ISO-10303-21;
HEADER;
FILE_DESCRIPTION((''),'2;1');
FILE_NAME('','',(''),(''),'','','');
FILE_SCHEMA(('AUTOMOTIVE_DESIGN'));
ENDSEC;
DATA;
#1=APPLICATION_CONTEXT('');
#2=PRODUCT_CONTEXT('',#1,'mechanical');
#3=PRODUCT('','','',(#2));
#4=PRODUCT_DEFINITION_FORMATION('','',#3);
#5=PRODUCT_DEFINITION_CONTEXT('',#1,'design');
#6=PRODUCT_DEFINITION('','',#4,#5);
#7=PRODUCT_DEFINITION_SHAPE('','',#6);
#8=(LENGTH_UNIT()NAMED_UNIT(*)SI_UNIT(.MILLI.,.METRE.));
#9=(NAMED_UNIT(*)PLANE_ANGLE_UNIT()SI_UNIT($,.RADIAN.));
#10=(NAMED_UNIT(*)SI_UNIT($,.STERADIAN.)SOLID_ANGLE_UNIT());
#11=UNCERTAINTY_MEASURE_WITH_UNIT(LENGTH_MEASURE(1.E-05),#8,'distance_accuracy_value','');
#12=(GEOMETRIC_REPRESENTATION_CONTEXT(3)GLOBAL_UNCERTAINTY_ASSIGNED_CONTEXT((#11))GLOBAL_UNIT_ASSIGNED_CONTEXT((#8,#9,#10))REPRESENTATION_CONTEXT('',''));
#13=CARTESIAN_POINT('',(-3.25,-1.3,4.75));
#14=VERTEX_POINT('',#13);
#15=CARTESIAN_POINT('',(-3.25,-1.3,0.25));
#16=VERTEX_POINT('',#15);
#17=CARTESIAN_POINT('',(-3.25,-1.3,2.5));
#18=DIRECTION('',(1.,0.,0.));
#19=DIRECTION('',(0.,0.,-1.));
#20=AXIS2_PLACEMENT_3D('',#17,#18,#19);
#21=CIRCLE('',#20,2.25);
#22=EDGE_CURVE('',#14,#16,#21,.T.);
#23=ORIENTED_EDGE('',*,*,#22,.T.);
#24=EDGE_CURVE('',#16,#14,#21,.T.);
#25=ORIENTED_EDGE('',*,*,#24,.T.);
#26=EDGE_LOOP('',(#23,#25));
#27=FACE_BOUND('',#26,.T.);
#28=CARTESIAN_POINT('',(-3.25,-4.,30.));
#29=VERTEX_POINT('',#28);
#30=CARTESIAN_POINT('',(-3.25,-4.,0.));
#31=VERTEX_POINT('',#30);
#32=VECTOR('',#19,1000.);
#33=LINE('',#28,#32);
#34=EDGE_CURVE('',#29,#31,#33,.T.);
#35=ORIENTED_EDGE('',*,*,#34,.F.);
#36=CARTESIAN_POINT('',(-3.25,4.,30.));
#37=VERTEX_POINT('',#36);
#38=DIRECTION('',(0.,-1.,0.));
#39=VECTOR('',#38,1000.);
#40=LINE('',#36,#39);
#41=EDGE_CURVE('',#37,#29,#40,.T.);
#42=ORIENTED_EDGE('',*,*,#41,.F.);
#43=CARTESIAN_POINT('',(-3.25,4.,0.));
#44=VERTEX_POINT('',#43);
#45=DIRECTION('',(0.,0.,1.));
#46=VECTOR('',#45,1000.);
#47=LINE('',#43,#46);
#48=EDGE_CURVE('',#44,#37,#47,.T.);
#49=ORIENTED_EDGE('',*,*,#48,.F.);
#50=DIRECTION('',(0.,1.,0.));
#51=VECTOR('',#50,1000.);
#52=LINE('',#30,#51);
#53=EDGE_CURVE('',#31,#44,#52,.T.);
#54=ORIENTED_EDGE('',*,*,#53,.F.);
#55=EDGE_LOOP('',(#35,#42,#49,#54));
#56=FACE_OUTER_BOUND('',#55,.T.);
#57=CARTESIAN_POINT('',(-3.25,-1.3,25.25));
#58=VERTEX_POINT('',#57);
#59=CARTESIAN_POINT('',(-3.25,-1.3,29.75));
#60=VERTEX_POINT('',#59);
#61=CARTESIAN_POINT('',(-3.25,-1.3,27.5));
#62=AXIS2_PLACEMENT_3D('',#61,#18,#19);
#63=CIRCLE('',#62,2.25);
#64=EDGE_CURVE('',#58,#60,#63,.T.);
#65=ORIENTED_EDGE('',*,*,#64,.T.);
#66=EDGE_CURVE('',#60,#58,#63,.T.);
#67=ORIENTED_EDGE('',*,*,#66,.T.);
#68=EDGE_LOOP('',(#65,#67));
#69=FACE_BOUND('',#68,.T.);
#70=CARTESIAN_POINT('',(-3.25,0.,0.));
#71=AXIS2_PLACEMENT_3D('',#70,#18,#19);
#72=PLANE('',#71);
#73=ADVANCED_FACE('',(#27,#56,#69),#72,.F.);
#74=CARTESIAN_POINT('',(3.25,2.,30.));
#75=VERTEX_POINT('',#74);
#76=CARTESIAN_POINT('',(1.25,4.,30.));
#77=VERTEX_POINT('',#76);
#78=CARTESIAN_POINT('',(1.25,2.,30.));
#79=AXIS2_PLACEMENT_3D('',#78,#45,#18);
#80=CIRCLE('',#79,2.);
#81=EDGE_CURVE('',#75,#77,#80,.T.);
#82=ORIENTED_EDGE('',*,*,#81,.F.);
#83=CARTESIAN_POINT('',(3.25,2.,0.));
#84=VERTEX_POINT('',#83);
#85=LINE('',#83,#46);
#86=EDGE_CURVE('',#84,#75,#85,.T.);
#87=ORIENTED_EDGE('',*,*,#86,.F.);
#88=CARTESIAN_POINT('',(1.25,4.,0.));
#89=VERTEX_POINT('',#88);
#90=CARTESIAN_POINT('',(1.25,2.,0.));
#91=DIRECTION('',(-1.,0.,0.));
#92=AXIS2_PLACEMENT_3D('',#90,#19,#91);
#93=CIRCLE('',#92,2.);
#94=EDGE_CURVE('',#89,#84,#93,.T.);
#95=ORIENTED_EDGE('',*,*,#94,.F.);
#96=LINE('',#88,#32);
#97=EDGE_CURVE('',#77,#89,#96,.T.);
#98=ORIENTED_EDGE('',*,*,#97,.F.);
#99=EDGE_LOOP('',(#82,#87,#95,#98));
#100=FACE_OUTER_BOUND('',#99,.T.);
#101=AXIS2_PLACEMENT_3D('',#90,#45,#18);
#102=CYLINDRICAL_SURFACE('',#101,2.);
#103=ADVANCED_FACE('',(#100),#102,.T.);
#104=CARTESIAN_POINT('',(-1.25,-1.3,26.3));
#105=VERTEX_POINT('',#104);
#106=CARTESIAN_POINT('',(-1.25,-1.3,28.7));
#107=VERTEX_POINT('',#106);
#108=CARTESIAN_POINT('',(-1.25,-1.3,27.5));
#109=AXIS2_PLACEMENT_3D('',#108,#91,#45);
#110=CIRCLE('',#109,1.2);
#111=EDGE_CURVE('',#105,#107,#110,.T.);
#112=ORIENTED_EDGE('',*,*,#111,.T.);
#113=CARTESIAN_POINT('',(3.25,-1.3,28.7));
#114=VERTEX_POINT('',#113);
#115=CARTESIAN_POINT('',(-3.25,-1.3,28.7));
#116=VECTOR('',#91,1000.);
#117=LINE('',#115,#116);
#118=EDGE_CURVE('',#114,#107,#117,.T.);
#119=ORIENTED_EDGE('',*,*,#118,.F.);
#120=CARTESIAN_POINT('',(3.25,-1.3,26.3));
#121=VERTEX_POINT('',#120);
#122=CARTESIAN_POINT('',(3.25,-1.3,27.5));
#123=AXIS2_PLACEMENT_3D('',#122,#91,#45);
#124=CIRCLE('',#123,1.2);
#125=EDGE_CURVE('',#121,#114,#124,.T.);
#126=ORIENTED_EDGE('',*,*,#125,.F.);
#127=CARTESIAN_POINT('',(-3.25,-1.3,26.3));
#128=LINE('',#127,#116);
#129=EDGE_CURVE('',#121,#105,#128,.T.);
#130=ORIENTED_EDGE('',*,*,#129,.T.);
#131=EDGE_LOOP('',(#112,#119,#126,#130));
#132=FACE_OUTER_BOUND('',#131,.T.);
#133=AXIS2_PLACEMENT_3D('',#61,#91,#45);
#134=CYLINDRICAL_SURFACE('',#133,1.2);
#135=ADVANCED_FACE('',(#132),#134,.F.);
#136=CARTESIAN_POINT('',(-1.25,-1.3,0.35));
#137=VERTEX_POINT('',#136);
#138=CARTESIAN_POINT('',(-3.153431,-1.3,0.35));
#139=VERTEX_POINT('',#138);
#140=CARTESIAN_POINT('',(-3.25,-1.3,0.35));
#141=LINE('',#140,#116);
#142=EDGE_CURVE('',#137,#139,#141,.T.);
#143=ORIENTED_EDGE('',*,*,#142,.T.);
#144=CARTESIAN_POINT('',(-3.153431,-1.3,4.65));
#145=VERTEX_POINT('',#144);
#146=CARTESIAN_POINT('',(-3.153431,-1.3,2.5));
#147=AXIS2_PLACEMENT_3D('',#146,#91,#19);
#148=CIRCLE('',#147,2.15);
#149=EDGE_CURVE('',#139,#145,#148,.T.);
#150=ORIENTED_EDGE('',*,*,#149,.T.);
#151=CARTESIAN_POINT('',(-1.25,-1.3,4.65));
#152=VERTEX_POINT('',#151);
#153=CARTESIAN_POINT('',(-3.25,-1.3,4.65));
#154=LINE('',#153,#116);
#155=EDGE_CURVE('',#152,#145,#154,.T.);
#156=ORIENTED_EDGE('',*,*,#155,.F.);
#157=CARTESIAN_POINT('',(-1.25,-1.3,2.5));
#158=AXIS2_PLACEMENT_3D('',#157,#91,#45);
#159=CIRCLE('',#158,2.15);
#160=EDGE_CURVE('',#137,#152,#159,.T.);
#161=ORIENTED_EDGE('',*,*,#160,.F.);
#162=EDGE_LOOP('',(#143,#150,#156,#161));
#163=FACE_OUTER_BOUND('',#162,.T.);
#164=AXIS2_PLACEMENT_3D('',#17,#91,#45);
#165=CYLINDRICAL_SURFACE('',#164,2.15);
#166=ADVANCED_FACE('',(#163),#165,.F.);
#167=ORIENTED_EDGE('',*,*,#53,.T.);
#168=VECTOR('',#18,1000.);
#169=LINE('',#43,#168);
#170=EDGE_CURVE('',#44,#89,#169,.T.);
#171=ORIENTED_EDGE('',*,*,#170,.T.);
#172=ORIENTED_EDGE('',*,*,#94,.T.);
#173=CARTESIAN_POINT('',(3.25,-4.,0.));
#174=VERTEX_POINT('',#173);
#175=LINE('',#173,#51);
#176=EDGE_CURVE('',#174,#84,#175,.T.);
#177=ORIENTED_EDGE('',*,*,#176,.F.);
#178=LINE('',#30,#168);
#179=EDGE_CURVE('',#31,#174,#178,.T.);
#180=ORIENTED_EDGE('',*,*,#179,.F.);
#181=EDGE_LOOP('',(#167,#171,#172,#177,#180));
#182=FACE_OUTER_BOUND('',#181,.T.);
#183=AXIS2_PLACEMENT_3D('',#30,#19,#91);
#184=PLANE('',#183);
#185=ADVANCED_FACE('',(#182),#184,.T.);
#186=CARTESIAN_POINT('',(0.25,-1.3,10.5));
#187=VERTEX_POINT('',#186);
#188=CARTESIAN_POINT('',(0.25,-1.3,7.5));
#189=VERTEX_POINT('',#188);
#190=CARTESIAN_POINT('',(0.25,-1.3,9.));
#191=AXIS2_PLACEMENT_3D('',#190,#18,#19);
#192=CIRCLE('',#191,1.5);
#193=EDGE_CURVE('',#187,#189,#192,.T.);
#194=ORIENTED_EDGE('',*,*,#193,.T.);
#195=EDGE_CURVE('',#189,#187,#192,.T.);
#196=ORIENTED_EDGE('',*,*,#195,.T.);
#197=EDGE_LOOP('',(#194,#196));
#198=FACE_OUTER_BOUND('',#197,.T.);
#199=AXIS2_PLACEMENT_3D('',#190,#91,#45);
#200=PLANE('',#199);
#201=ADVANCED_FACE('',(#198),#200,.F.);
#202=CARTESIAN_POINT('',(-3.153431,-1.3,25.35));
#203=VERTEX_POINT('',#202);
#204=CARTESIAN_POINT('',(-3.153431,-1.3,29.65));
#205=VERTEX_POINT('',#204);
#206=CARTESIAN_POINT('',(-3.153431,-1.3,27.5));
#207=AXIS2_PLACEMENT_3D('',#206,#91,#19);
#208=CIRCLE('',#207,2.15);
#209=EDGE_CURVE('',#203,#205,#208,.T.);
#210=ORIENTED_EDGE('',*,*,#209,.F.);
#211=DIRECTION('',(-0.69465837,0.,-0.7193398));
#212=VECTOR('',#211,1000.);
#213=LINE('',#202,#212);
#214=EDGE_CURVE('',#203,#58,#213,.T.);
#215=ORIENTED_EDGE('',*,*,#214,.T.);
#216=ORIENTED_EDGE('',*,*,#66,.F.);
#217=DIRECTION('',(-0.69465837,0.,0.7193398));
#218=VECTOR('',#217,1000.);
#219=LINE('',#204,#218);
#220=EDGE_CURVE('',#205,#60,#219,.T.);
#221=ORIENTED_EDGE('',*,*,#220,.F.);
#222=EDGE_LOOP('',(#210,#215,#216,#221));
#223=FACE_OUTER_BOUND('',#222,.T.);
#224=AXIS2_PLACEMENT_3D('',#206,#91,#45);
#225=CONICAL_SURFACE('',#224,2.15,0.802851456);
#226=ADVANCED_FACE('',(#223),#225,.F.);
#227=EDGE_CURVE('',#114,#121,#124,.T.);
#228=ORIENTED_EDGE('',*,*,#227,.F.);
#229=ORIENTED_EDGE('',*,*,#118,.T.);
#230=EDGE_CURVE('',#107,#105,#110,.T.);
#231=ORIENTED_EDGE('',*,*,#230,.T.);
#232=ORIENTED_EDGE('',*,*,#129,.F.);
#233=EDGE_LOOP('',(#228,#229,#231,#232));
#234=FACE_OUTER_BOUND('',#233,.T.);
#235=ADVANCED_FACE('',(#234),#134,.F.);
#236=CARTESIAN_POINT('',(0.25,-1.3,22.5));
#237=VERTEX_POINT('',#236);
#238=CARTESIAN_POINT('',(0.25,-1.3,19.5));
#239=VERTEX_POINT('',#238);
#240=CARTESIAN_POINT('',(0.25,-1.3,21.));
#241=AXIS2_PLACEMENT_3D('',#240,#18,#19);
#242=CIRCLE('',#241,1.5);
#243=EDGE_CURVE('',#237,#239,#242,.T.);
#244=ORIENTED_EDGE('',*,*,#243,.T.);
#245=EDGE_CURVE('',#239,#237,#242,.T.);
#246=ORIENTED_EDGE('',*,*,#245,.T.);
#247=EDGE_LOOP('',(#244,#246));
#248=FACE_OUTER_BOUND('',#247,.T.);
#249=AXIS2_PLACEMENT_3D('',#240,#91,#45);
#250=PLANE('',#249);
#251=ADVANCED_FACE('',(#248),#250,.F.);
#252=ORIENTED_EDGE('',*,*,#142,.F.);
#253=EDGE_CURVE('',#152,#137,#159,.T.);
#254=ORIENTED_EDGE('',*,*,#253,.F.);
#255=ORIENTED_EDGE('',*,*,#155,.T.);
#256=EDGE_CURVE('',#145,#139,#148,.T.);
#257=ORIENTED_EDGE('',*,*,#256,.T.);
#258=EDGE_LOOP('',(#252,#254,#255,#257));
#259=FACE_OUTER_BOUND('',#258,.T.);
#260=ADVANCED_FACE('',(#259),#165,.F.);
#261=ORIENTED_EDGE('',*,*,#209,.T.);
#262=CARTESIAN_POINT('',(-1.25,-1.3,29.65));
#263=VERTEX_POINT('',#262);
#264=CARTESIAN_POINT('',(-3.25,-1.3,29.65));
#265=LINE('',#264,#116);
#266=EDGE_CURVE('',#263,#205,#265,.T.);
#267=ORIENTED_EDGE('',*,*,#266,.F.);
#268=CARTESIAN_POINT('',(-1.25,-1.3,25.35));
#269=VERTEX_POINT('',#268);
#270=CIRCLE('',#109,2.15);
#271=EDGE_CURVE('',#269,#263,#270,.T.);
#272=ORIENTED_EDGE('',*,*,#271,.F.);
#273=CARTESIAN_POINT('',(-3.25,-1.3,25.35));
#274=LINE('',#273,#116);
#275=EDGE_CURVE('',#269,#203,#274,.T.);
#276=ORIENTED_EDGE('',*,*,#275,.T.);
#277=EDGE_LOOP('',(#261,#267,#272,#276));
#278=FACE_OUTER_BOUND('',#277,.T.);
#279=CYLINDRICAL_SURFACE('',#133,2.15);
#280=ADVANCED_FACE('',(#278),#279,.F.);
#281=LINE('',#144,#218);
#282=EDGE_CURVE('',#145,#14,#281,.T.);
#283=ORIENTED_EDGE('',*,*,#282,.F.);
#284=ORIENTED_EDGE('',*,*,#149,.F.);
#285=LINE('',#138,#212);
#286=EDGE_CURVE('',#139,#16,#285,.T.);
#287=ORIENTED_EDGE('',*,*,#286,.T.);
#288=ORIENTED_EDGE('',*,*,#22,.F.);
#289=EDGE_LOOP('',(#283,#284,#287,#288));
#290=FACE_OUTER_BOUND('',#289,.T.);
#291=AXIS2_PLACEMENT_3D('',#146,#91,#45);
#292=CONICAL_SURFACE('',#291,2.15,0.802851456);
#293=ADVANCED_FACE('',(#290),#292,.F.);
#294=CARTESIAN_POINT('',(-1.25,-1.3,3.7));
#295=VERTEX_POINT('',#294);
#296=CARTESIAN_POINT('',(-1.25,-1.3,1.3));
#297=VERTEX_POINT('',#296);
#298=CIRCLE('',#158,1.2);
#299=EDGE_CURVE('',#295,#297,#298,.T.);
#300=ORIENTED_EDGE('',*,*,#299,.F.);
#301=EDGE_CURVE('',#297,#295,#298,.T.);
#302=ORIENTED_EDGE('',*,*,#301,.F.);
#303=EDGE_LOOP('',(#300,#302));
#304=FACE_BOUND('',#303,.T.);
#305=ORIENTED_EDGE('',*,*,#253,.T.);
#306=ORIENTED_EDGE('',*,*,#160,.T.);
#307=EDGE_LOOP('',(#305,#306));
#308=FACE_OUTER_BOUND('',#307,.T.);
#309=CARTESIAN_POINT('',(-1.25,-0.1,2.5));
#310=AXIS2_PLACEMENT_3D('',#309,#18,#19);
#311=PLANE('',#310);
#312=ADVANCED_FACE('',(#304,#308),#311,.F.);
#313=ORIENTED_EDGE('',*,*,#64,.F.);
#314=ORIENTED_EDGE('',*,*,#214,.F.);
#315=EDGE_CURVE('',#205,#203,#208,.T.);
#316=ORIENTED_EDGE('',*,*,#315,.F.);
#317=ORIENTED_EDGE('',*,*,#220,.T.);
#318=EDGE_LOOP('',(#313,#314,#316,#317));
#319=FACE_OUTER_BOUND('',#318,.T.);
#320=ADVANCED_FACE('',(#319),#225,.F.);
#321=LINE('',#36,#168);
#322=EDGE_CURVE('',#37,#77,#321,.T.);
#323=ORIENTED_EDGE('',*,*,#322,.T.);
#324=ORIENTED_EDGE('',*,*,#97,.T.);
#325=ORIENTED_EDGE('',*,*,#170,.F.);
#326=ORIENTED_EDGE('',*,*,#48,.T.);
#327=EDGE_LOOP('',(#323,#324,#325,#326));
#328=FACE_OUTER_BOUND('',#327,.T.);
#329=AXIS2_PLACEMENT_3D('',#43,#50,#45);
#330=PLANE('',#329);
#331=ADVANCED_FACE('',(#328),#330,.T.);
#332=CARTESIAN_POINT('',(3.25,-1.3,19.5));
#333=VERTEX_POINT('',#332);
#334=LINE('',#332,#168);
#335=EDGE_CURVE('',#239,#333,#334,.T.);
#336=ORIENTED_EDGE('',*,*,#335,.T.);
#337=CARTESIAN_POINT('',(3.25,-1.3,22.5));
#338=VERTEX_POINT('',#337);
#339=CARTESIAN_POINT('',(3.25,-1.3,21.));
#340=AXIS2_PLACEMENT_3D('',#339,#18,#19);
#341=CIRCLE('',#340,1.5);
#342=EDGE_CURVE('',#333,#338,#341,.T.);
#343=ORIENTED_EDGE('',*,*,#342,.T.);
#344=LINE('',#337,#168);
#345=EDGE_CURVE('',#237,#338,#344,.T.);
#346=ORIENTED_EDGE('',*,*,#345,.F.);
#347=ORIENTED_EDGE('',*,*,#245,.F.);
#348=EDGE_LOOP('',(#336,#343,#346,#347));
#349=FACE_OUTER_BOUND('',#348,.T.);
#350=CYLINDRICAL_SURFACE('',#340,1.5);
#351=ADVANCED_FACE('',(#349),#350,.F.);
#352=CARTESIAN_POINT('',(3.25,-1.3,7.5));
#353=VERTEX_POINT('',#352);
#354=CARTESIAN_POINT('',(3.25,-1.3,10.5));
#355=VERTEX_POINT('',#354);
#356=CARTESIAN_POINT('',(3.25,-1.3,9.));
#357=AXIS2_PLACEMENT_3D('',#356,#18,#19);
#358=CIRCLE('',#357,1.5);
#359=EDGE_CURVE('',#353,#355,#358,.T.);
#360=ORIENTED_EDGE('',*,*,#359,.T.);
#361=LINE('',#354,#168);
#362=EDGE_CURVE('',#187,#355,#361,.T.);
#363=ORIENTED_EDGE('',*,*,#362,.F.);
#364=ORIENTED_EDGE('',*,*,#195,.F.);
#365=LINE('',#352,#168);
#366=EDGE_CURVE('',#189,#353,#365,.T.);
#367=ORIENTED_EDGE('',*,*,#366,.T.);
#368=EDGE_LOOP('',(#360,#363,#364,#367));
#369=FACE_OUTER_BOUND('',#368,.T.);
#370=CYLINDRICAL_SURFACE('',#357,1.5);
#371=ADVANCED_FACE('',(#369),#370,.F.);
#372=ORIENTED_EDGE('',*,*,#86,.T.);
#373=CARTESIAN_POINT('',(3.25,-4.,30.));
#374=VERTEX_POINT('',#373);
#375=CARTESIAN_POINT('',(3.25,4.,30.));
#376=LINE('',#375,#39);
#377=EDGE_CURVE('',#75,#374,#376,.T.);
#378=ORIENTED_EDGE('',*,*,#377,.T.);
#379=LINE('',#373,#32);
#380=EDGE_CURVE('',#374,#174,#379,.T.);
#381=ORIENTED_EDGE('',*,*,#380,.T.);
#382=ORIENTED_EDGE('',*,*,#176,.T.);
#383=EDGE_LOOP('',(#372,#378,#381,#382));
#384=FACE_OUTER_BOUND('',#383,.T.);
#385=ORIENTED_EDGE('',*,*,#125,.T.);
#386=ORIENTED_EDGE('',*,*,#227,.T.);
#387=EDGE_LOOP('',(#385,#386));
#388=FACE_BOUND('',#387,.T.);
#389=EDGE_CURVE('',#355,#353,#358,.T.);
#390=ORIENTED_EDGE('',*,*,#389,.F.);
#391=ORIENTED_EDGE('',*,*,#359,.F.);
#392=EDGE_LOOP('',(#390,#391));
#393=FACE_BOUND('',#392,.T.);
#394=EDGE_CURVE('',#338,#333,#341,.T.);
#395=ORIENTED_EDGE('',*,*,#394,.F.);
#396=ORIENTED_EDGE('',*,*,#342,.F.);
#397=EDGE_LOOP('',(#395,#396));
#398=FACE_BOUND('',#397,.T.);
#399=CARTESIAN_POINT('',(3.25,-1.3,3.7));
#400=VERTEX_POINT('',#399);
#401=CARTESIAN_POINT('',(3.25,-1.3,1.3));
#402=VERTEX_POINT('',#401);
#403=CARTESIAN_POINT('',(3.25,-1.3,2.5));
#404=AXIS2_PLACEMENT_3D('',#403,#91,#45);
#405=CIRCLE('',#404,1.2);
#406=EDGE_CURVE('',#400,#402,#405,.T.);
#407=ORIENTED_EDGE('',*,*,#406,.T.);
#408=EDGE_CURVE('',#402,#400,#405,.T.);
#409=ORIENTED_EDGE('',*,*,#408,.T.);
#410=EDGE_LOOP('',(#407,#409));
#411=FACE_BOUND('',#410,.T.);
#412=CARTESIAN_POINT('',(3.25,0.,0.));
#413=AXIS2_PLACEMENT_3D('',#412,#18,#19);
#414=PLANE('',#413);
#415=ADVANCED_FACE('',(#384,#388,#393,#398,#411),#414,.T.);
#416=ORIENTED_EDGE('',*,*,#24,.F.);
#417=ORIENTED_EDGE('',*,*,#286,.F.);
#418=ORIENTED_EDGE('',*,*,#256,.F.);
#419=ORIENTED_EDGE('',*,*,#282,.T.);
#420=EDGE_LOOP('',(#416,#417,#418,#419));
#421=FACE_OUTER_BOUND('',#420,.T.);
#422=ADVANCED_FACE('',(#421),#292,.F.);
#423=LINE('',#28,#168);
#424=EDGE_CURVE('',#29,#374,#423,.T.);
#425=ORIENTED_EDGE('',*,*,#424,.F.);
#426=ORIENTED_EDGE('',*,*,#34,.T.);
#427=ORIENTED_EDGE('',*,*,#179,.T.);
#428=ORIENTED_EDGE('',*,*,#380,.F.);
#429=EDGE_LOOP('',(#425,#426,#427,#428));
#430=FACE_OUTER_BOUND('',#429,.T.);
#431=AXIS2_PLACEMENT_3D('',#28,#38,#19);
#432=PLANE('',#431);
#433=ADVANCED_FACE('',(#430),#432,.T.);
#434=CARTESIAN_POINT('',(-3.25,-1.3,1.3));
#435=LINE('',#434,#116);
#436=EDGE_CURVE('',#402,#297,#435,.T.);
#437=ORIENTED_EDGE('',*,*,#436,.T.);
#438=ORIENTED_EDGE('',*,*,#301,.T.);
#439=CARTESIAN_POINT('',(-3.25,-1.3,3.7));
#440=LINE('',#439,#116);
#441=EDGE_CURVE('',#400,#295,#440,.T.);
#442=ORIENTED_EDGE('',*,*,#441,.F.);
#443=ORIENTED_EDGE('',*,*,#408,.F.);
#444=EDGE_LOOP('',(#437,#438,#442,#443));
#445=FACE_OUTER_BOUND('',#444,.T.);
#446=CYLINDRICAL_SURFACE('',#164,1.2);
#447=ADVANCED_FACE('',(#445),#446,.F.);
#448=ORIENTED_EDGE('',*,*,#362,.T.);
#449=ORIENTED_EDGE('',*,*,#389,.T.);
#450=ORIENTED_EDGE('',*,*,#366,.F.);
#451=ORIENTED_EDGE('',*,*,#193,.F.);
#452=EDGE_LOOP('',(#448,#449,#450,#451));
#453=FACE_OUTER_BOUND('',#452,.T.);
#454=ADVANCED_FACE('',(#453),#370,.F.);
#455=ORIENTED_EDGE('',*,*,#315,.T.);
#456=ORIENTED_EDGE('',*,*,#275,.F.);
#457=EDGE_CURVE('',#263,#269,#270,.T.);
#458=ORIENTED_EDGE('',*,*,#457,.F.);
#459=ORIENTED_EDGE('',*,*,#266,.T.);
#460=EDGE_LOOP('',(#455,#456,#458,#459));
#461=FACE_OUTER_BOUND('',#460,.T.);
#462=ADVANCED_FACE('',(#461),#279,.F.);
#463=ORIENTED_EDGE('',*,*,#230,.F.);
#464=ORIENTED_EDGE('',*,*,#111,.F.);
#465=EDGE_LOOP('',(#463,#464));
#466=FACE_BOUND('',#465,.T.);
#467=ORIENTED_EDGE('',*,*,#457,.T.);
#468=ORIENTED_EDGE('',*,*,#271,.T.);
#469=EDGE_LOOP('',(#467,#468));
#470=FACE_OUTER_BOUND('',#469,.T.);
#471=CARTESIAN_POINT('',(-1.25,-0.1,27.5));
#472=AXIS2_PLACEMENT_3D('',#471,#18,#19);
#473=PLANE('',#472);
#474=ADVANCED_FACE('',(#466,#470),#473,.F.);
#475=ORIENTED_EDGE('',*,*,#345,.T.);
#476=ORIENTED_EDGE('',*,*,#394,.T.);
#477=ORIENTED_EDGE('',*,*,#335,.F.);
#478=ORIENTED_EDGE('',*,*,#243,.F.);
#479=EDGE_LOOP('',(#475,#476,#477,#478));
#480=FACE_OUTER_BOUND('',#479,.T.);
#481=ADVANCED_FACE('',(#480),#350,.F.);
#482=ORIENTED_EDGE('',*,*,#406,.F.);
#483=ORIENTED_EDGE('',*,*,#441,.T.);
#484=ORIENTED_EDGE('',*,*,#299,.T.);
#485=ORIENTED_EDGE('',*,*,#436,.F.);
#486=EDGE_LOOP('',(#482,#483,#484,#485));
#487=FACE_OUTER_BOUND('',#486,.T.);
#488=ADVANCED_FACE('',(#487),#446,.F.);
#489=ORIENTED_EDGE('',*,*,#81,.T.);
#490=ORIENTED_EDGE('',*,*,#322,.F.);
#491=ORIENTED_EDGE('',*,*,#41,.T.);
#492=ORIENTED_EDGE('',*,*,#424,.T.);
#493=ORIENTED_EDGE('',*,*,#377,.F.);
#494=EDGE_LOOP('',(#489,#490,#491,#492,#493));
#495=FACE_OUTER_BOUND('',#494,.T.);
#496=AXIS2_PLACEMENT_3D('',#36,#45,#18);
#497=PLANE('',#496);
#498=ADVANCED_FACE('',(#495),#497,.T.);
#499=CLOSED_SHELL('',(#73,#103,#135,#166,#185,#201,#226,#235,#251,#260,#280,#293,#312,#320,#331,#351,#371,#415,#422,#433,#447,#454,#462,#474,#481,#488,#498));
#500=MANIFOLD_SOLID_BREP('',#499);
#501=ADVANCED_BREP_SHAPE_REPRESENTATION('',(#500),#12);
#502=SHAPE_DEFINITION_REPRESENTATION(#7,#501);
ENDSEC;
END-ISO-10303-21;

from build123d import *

# Parameters (mm, degrees)
SKETCH_1_W                   = 30
SKETCH_1_H                   = 8
EXTRUDE_1_DEPTH              = 6.5
HOLE_WIZARD_3_0_3_1_D        = 3
HOLE_WIZARD_3_0_3_1_DEPTH    = 3
HOLE_WIZARD_M2_1_D           = 2.4
HOLE_WIZARD_M2_1_CBORE_D     = 4.3
HOLE_WIZARD_M2_1_CBORE_DEPTH = 2
CHAMFER_1_SIZE               = 0.1
CHAMFER_1_SIZE2              = 0.096568877
FILLET_1_R                   = 2


with BuildPart() as part:
    # 草图1 → 凸台-拉伸1 (new body)
    with BuildSketch(Plane(origin=(3.25, 0, 0), x_dir=(0, 0, -1), z_dir=(1, 0, 0))):
        with Locations((-15, 0)):
            Rectangle(SKETCH_1_W, SKETCH_1_H)
    extrude(amount=-EXTRUDE_1_DEPTH)

    # Ø3.0 (3) 直径孔1
    with Locations(Plane(origin=(3.25, 0, 0), x_dir=(0, 0, -1), z_dir=(1, 0, 0))):
        with Locations((-9, -1.3), (-21, -1.3)):
            Hole(HOLE_WIZARD_3_0_3_1_D / 2, depth=HOLE_WIZARD_3_0_3_1_DEPTH)

    # M2 六角头机械螺钉的柱形沉头孔1 (through all)
    with Locations(Plane.ZY.offset(3.25)):
        with Locations((27.5, -1.3), (2.5, -1.3)):
            CounterBoreHole(HOLE_WIZARD_M2_1_D / 2, HOLE_WIZARD_M2_1_CBORE_D / 2, HOLE_WIZARD_M2_1_CBORE_DEPTH)

    # 倒角1
    chamfer_1_edges = [part.edges().sort_by_distance(p)[0] for p in [
        (-3.25, -1.3, 0.35),
        (-3.25, -1.3, 25.35),
    ]]
    chamfer_1_side = [part.faces().sort_by_distance(p)[0] for p in [
        (-3.25, 0.178981568, 15),
    ]]
    chamfer(chamfer_1_edges, length=CHAMFER_1_SIZE, length2=CHAMFER_1_SIZE2, reference=chamfer_1_side[0])

    # 圆角1
    fillet_1_edges = [part.edges().sort_by_distance(p)[0] for p in [
        (3.25, 4, 15),
    ]]
    fillet(fillet_1_edges, radius=FILLET_1_R)


solid = part.part
